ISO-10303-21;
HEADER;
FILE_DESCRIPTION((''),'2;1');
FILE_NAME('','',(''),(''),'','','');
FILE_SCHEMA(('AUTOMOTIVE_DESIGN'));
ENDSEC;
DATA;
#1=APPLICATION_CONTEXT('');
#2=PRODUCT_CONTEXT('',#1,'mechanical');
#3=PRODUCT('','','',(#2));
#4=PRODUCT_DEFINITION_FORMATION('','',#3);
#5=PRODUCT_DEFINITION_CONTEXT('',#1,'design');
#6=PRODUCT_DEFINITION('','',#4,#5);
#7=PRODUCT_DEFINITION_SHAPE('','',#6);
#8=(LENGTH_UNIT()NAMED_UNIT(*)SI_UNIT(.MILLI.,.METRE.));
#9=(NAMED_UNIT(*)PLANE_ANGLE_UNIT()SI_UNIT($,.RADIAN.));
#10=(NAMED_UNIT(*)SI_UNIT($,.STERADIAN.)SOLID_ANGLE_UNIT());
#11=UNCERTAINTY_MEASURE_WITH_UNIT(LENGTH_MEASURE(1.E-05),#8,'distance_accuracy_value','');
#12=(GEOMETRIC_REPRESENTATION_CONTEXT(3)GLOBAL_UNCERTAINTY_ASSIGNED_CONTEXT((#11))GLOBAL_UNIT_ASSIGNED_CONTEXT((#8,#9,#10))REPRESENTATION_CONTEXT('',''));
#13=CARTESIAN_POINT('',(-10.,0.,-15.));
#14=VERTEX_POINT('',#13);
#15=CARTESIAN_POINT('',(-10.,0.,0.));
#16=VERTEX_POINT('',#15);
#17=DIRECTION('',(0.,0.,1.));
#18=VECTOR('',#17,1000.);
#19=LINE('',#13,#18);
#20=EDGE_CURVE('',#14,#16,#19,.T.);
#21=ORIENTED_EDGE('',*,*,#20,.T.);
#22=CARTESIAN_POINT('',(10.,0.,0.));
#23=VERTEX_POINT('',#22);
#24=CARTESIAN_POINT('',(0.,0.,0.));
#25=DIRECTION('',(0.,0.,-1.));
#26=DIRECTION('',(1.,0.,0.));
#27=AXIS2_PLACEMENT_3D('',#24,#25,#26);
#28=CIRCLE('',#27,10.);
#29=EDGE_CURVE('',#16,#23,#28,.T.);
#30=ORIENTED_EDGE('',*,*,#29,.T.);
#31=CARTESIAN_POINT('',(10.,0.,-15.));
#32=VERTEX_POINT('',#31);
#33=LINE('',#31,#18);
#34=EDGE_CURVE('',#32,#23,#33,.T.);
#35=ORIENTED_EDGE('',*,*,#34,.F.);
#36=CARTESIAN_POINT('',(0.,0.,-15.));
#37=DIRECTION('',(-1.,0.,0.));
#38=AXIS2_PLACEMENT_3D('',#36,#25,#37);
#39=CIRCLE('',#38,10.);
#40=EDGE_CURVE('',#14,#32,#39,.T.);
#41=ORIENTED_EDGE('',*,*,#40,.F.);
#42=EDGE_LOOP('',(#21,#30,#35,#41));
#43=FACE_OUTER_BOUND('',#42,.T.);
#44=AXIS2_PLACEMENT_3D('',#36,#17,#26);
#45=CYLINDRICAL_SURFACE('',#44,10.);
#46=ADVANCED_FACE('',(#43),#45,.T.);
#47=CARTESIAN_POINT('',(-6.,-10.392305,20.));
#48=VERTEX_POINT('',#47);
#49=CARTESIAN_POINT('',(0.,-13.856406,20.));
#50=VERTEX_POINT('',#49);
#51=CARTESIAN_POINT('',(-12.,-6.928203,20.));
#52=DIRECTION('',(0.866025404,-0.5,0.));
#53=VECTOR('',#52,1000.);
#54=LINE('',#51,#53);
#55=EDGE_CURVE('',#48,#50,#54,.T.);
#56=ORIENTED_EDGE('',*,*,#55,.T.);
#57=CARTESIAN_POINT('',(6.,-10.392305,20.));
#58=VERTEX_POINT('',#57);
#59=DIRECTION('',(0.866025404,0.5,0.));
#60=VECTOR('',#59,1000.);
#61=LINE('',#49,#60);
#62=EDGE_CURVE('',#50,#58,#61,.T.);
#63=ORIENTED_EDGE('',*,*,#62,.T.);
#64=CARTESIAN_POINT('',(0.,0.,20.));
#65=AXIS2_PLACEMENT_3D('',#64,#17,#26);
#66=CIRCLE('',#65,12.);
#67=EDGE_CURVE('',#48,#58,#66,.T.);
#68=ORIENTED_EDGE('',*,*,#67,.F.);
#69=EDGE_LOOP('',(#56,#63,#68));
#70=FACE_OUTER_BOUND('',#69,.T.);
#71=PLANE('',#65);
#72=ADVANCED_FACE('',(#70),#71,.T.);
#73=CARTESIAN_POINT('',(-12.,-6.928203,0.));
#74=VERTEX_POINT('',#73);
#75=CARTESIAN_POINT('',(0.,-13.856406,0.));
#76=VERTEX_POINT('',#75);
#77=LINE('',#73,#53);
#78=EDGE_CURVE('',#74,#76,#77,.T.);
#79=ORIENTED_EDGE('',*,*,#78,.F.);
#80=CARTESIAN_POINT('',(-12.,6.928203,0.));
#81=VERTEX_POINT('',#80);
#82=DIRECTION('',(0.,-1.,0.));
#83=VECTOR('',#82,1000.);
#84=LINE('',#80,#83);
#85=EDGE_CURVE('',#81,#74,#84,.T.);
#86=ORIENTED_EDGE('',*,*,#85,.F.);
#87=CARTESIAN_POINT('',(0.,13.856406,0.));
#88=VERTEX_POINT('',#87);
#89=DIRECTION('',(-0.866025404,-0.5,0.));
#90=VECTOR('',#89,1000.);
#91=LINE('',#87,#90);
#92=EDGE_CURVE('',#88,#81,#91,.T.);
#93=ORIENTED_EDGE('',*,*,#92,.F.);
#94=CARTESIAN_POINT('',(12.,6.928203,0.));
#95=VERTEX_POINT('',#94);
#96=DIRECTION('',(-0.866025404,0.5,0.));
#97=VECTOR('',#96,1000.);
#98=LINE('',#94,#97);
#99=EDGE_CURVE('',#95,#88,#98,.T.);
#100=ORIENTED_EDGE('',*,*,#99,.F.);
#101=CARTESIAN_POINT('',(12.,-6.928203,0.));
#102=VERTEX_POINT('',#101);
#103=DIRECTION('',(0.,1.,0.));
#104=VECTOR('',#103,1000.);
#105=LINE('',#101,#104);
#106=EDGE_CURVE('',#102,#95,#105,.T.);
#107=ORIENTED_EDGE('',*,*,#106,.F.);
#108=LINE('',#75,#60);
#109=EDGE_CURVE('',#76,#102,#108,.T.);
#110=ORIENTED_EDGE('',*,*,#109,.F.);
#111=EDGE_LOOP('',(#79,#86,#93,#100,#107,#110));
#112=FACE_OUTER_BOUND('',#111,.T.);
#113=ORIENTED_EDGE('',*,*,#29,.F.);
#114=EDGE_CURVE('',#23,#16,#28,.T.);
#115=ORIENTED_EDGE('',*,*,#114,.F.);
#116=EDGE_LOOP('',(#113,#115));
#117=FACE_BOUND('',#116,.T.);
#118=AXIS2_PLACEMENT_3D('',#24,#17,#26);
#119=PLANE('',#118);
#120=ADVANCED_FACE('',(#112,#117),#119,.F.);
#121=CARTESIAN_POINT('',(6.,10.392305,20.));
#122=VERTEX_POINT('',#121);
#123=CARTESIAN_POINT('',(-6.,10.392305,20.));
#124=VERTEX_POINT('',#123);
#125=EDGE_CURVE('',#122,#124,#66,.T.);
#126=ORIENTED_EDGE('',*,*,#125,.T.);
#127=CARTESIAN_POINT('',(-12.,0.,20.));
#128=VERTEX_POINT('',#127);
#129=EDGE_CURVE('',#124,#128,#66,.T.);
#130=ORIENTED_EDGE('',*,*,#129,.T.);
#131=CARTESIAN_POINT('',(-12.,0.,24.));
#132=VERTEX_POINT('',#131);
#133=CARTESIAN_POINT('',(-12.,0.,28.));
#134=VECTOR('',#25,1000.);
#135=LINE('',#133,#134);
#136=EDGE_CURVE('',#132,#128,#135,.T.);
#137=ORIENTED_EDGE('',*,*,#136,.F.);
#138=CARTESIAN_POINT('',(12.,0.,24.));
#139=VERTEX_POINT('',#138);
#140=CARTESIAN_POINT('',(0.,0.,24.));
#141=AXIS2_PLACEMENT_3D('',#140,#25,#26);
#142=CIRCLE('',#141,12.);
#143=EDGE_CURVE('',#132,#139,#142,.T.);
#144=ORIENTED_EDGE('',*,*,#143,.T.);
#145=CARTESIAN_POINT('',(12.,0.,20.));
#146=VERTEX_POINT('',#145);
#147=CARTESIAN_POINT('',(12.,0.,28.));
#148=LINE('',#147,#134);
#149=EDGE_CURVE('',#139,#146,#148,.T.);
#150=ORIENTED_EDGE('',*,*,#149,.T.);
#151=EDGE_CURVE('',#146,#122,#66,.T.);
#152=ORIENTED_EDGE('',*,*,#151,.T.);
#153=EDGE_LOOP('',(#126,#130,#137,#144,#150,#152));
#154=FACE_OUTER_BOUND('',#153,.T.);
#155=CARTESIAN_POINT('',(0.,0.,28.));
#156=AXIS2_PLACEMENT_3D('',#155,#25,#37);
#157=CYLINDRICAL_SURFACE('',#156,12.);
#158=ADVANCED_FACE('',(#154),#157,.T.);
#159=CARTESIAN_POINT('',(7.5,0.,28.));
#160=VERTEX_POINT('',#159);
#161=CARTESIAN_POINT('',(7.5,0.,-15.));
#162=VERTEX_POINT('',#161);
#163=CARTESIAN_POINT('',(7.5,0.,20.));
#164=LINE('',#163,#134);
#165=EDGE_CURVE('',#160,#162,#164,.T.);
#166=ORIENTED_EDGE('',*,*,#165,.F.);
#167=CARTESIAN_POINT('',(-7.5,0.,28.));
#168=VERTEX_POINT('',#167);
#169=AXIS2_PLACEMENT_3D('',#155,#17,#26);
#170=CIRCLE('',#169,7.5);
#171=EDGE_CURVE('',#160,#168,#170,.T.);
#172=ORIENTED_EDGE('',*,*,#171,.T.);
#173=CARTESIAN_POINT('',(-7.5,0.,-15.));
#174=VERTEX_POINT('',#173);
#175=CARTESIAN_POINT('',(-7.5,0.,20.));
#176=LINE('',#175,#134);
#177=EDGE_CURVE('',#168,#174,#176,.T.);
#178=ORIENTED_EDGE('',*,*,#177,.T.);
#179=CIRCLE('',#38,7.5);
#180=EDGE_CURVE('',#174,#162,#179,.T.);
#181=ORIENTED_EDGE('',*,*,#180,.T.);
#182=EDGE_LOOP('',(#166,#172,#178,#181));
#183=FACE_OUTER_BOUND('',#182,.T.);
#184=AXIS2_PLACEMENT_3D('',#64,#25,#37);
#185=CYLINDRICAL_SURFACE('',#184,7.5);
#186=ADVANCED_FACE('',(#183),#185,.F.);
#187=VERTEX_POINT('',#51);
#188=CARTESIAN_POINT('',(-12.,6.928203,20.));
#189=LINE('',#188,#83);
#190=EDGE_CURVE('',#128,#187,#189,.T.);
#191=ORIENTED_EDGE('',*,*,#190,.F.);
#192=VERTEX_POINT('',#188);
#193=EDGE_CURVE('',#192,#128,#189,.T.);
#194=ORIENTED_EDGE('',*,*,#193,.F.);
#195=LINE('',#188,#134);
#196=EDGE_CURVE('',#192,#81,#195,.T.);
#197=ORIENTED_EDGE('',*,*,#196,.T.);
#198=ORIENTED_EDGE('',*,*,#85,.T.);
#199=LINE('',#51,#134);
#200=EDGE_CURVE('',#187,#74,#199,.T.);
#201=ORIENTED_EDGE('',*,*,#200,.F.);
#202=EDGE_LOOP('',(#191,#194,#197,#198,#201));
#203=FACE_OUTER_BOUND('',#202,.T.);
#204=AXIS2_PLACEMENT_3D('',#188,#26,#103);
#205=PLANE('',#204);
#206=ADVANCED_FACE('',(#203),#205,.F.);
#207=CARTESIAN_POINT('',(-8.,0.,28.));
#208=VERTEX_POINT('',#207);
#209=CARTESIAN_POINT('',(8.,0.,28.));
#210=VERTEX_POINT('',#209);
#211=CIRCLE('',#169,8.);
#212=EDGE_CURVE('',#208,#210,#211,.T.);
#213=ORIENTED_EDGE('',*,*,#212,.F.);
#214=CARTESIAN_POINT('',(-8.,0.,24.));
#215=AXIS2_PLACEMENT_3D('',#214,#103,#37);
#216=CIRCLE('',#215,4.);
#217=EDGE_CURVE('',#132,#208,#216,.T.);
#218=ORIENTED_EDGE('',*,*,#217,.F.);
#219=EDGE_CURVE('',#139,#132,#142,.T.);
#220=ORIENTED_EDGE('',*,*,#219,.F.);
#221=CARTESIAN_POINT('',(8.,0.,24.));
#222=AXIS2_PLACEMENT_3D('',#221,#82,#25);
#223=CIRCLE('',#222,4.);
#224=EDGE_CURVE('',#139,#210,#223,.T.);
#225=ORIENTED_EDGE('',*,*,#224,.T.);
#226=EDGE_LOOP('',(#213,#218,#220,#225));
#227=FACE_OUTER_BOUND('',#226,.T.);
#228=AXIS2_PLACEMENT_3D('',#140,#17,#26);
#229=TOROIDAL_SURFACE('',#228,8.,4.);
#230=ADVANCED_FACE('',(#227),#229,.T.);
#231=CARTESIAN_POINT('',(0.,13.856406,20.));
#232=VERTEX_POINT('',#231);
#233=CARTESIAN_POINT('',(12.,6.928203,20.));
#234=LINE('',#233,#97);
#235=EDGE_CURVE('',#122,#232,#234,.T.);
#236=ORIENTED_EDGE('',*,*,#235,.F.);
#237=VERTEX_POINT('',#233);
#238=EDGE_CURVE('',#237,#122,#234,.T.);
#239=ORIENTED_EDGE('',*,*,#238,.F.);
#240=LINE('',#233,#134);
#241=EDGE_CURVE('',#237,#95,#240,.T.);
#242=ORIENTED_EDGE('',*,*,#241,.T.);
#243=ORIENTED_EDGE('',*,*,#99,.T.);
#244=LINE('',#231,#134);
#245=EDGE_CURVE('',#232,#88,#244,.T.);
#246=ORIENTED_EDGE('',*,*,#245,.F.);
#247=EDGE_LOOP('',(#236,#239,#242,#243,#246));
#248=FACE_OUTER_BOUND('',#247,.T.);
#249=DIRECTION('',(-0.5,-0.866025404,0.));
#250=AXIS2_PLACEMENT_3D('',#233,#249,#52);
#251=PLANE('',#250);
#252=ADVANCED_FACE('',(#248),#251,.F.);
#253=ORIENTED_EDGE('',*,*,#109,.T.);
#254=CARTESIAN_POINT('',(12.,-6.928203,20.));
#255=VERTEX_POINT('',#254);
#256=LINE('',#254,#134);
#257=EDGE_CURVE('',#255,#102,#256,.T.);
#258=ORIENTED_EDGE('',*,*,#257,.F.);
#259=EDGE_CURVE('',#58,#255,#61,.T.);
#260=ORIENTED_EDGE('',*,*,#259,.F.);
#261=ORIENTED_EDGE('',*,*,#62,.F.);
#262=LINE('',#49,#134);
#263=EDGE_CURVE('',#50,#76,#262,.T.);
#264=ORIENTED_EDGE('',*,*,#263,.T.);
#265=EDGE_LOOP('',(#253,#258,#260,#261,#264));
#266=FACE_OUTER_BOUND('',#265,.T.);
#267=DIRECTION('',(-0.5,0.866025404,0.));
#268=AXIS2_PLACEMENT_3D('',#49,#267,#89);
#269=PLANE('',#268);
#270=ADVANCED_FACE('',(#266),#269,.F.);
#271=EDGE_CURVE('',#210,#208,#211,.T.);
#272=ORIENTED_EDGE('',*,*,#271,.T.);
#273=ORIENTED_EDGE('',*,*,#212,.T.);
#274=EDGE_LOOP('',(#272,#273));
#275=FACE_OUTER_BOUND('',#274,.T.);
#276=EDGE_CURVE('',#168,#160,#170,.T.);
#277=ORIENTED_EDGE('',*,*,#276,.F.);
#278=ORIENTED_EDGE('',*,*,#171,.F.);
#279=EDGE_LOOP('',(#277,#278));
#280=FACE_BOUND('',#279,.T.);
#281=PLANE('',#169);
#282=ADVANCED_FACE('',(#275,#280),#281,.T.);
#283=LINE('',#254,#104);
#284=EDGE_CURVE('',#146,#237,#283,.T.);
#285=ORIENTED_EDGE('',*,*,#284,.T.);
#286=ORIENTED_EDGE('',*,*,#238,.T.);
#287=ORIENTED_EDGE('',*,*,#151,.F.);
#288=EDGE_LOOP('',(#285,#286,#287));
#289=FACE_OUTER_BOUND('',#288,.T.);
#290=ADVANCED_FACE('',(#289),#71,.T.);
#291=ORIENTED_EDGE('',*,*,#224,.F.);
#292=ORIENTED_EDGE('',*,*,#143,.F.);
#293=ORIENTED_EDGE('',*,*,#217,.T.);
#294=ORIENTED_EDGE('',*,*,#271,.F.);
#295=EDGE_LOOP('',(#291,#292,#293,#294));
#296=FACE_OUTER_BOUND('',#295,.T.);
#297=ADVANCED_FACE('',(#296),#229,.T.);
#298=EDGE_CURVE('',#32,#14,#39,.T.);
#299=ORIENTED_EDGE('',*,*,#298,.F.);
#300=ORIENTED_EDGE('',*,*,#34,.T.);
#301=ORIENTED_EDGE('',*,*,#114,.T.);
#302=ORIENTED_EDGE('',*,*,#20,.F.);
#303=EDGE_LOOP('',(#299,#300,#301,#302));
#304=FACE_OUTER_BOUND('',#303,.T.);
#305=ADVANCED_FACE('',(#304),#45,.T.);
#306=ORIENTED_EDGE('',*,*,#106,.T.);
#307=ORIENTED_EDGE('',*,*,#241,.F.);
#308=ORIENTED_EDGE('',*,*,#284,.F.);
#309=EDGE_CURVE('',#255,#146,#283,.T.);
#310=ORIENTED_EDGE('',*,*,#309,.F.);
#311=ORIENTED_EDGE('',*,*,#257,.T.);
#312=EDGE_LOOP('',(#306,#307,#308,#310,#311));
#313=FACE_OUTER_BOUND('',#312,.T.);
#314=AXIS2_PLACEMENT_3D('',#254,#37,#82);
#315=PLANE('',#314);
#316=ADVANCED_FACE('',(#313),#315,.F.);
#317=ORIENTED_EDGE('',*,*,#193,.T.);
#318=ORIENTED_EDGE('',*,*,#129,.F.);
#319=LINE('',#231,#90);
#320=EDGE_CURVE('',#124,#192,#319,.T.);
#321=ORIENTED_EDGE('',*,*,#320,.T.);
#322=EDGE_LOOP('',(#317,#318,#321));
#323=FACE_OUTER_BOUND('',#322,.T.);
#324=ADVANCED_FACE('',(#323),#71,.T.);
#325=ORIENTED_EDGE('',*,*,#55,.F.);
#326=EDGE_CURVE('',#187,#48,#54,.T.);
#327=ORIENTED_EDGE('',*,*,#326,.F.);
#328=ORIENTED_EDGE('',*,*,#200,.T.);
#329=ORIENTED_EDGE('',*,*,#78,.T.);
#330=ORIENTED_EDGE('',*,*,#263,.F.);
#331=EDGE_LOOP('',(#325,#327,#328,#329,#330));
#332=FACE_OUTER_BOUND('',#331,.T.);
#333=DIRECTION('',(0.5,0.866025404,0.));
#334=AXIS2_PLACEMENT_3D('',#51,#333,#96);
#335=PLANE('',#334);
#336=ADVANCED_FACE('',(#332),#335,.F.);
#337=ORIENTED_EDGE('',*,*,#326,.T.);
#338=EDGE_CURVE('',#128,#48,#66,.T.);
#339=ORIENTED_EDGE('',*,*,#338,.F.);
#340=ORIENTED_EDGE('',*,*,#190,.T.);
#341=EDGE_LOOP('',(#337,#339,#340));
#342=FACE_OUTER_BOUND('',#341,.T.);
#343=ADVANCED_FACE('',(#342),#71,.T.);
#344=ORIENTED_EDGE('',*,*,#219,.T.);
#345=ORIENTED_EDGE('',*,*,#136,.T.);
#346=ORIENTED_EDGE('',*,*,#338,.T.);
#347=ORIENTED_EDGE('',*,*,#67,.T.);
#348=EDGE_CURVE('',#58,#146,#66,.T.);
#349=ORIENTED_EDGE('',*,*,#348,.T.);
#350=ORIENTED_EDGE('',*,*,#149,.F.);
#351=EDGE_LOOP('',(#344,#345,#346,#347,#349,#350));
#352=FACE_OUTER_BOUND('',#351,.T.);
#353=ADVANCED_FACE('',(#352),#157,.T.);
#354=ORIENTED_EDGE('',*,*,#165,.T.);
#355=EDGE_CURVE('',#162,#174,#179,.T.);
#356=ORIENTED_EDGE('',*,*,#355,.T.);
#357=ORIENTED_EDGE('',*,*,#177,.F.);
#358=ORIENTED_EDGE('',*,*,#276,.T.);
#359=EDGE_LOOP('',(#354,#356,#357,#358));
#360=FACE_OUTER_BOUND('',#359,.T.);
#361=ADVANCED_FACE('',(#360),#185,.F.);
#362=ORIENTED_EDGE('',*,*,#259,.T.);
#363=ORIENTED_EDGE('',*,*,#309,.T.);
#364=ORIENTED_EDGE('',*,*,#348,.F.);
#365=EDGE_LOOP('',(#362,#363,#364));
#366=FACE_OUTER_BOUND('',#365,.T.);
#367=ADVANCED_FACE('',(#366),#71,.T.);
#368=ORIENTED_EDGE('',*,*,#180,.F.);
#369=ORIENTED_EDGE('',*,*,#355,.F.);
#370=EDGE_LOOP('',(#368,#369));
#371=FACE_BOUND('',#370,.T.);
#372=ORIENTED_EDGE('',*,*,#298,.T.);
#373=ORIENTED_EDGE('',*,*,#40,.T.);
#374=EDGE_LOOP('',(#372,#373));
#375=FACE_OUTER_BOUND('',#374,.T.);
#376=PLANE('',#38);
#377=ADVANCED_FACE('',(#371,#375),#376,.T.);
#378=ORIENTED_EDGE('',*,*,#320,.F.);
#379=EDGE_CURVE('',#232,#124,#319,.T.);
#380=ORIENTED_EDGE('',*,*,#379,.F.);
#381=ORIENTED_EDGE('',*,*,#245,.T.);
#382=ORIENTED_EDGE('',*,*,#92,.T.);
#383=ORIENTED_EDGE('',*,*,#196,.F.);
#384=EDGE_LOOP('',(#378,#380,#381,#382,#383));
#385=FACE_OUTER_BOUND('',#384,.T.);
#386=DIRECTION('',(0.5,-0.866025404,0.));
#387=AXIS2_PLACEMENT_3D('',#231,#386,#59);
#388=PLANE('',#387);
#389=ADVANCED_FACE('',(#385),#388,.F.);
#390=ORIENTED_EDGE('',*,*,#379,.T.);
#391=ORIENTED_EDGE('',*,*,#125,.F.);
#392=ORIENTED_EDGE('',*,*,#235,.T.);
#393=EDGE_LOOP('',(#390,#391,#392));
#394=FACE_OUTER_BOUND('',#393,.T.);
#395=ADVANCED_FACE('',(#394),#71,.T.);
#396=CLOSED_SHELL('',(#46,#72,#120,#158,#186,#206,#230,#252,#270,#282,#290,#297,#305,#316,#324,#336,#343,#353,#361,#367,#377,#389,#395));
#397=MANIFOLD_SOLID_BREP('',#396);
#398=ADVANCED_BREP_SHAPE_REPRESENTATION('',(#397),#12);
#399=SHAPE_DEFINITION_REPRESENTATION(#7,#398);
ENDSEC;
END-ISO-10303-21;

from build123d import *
from build123d.topology import SkipClean

# Parameters (mm, degrees)
SKETCH_1_R      = 7.5
EXTRUDE_1_DEPTH = 20
SKETCH_3_R      = 12
SKETCH_3_R_2    = 7.5
EXTRUDE_3_DEPTH = 8
FILLET_1_R      = 4
EXTRUDE_START   = 15
SKETCH_4_R      = 10
SKETCH_4_R_2    = 7.5
EXTRUDE_4_DEPTH = 15


with BuildPart() as part:
    # 草图1 → 凸台-拉伸1 (new body)
    with BuildSketch(Plane.XY):
        Polygon((0, 13.856406461), (-12, 6.92820323), (-12, -6.92820323), (0, -13.856406461), (12, -6.92820323), (12, 6.92820323), align=None)
        Circle(SKETCH_1_R, mode=Mode.SUBTRACT)
    extrude(amount=EXTRUDE_1_DEPTH)

    # 草图3 → 凸台-拉伸3 (add)
    with BuildSketch(Plane.XY.offset(20)):
        Circle(SKETCH_3_R)
        Circle(SKETCH_3_R_2, mode=Mode.SUBTRACT)
    extrude(amount=EXTRUDE_3_DEPTH)

    # 圆角1
    fillet_1_edges = [part.edges().sort_by_distance(p)[0] for p in [
        (-12, 0, 28),
    ]]
    fillet(fillet_1_edges, radius=FILLET_1_R)

    # 草图4 → 凸台-拉伸4 (add)
    with SkipClean():  # the faces are left unmerged after this step: merging them gives an invalid solid
        with BuildSketch(Plane(origin=(0, 0, 0), x_dir=(-1, 0, 0), z_dir=(0, 0, -1)).offset(EXTRUDE_START)):
            with Locations(Location((0, 0, 0), (0, 0, 180))):
                Circle(SKETCH_4_R)
            Circle(SKETCH_4_R_2, mode=Mode.SUBTRACT)
        extrude(amount=-EXTRUDE_4_DEPTH)


solid = part.part
